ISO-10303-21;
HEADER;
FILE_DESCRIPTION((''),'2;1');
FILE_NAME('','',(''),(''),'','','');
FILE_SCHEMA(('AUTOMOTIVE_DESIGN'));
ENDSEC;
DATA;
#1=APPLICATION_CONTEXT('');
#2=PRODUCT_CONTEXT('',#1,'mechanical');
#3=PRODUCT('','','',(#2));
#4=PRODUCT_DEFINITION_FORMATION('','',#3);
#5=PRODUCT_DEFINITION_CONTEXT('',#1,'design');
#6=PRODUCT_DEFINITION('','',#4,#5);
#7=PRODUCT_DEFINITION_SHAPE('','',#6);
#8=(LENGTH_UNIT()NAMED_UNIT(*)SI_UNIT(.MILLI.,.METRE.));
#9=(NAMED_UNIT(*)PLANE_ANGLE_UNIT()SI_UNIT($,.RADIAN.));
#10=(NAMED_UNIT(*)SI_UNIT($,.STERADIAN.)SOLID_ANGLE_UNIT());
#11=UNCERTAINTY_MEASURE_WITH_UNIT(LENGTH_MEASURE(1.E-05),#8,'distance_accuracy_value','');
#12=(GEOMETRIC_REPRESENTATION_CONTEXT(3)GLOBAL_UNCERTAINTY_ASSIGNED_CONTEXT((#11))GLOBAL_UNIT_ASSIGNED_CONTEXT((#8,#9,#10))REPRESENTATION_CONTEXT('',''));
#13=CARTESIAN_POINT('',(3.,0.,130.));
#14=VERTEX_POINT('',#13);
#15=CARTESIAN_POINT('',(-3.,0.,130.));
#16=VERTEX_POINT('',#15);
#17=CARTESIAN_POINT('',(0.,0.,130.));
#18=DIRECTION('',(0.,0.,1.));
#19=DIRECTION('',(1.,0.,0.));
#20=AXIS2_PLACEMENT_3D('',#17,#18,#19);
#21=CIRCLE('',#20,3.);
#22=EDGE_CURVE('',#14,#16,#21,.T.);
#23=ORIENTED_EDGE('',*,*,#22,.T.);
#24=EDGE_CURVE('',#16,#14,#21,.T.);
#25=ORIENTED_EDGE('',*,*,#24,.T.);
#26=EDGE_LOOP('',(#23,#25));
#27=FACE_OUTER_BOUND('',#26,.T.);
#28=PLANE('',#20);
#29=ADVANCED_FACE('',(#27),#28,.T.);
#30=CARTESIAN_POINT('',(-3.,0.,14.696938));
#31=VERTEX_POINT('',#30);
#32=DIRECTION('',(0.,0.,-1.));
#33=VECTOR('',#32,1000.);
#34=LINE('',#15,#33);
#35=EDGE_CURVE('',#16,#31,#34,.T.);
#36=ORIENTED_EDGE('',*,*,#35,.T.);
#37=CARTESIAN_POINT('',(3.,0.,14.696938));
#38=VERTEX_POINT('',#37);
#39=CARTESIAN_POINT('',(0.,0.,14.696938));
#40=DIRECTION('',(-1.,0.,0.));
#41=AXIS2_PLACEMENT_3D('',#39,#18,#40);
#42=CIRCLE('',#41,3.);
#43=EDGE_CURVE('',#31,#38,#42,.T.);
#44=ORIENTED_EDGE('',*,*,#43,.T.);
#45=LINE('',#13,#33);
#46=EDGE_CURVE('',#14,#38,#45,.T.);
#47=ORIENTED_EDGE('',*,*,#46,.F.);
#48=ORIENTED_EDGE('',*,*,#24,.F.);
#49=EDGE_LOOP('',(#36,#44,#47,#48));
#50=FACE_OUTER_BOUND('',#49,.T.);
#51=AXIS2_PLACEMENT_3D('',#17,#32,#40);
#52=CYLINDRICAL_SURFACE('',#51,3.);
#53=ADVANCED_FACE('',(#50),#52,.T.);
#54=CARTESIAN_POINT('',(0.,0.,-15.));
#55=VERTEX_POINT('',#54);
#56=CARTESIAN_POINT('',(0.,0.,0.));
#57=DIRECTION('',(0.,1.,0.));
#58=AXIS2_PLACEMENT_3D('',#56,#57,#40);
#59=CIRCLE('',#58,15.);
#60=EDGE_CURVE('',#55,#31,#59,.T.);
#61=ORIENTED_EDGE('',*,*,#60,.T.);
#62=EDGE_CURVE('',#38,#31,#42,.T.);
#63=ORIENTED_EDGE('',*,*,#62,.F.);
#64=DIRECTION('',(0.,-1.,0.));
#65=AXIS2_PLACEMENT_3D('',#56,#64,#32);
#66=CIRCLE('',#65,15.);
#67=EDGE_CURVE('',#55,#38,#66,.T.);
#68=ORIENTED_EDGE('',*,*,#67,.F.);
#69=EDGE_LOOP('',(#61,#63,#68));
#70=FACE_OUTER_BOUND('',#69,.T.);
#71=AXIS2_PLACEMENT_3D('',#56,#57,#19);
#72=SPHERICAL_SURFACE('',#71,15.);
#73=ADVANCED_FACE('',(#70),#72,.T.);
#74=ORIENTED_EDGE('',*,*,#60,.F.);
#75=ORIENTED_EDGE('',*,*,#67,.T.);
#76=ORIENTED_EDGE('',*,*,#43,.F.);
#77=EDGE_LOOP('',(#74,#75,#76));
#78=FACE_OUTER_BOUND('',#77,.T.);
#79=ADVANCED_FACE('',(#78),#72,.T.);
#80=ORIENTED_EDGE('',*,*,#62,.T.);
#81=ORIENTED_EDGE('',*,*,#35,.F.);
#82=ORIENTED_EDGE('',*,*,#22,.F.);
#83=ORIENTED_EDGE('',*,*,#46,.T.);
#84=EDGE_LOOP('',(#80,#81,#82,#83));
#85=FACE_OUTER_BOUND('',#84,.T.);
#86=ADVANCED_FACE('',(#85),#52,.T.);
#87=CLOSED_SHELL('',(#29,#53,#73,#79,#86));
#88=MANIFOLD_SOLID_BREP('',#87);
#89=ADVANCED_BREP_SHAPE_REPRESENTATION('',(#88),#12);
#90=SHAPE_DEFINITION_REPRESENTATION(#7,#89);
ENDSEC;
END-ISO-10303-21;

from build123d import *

# Parameters (mm, degrees)
SKETCH2_R           = 3
BOSS_EXTRUDE1_DEPTH = 130


with BuildPart() as part:
    # Sketch1 → Revolve3 (revolve)
    with BuildSketch(Plane(origin=(0, 0, 0), x_dir=(1, 0, 0), z_dir=(0, 1, 0))):
        with BuildLine():
            Line((0, 15), (0, -15))
            ThreePointArc((0, -15), (-15, 0), (0, 15))
        make_face()
    revolve(axis=Axis((0, 0, 1000), (0, 0, -1)))

    # Sketch2 → Boss-Extrude1 (add)
    with BuildSketch(Plane.XY):
        Circle(SKETCH2_R)
    extrude(amount=BOSS_EXTRUDE1_DEPTH)


solid = part.part
